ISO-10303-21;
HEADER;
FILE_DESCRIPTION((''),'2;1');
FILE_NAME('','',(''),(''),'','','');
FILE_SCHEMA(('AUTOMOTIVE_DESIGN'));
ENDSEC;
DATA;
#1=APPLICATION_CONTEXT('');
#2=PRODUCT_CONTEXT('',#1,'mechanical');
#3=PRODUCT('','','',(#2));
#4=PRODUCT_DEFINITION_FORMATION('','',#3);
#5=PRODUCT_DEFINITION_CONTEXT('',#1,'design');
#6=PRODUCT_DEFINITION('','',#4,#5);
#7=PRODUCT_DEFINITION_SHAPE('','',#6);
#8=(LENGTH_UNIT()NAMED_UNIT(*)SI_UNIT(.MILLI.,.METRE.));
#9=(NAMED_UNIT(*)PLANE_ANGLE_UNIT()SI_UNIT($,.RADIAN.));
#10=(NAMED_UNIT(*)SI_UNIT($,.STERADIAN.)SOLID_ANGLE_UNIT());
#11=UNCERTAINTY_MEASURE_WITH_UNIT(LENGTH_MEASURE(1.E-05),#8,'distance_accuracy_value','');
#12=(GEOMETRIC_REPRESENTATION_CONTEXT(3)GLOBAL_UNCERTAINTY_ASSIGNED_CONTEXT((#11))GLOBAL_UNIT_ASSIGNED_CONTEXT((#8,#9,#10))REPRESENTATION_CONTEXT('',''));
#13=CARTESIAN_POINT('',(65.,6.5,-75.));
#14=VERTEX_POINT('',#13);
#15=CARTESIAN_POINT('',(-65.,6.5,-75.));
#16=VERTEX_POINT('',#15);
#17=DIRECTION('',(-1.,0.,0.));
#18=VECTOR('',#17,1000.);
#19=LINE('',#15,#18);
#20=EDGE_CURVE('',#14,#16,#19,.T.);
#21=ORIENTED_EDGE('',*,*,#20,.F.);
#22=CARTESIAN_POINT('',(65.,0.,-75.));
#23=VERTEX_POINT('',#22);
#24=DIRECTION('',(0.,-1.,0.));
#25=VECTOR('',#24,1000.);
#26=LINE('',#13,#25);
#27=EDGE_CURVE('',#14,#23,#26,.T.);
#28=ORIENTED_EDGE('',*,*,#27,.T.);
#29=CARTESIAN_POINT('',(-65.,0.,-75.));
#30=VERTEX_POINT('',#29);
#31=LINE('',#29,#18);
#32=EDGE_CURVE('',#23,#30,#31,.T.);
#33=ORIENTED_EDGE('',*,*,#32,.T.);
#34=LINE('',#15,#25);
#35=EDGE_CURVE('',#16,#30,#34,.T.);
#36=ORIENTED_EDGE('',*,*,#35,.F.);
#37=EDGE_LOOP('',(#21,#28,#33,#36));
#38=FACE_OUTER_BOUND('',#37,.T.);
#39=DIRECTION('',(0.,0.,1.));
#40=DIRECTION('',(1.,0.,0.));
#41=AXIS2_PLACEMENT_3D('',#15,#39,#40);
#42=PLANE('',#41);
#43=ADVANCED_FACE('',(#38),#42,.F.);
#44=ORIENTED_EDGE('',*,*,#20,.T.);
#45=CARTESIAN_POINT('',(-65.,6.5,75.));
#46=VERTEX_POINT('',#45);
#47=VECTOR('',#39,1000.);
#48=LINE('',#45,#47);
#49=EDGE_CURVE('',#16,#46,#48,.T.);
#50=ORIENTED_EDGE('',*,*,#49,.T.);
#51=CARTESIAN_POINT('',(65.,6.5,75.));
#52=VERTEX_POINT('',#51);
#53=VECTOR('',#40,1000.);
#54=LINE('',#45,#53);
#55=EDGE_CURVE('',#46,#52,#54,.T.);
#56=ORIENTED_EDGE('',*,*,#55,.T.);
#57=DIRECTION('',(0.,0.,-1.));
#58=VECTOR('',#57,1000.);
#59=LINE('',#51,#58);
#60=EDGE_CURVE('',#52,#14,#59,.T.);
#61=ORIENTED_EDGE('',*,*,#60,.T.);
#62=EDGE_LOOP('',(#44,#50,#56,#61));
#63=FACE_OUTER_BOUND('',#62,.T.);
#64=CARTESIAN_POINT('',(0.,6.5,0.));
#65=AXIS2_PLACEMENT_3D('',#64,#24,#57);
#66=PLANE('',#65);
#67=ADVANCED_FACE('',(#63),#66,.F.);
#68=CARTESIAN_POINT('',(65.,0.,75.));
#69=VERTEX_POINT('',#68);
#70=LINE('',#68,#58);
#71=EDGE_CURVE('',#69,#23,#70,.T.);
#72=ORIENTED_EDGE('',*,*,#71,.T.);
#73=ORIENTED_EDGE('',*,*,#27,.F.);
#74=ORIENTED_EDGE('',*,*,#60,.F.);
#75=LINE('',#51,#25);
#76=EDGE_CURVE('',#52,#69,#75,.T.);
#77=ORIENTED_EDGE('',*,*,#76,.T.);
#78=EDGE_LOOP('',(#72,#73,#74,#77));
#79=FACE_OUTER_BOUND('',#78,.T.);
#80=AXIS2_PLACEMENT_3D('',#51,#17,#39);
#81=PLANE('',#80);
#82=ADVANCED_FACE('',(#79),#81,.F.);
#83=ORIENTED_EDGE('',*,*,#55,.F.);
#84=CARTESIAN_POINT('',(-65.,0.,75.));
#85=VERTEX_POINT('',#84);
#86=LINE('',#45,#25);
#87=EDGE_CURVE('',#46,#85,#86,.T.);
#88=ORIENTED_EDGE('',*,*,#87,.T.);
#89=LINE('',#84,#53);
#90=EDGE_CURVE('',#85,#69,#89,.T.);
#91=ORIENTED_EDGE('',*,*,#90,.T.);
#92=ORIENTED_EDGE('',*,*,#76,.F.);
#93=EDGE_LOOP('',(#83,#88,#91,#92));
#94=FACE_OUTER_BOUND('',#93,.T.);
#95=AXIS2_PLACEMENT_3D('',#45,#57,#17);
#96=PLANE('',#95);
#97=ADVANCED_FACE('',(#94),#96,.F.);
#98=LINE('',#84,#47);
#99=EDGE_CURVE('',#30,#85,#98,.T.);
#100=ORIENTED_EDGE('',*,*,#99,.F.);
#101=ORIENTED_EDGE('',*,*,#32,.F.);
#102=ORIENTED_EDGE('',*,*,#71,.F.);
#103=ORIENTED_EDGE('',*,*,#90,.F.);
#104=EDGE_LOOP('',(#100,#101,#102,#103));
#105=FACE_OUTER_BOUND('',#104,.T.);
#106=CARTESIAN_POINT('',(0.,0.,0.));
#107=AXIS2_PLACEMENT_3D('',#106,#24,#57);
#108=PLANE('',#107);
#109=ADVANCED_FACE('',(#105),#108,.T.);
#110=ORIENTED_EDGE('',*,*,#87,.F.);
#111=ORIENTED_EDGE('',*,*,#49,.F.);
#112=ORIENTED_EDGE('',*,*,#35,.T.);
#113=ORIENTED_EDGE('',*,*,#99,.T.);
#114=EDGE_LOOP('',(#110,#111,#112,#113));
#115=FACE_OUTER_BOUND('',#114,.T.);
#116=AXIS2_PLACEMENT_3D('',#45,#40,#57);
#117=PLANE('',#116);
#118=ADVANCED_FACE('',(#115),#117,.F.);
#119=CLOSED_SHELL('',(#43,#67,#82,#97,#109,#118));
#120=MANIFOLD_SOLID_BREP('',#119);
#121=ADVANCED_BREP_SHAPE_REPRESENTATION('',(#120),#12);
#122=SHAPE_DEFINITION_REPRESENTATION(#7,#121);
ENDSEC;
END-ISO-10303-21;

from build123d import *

# Parameters (mm, degrees)
SKETCH1_W           = 130
SKETCH1_H           = 150
BOSS_EXTRUDE1_DEPTH = 6.5


with BuildPart() as part:
    # Sketch1 → Boss-Extrude1 (new body)
    with BuildSketch(Plane(origin=(0, 0, 0), x_dir=(1, 0, 0), z_dir=(0, 1, 0))):
        Rectangle(SKETCH1_W, SKETCH1_H)
    extrude(amount=BOSS_EXTRUDE1_DEPTH)


solid = part.part
